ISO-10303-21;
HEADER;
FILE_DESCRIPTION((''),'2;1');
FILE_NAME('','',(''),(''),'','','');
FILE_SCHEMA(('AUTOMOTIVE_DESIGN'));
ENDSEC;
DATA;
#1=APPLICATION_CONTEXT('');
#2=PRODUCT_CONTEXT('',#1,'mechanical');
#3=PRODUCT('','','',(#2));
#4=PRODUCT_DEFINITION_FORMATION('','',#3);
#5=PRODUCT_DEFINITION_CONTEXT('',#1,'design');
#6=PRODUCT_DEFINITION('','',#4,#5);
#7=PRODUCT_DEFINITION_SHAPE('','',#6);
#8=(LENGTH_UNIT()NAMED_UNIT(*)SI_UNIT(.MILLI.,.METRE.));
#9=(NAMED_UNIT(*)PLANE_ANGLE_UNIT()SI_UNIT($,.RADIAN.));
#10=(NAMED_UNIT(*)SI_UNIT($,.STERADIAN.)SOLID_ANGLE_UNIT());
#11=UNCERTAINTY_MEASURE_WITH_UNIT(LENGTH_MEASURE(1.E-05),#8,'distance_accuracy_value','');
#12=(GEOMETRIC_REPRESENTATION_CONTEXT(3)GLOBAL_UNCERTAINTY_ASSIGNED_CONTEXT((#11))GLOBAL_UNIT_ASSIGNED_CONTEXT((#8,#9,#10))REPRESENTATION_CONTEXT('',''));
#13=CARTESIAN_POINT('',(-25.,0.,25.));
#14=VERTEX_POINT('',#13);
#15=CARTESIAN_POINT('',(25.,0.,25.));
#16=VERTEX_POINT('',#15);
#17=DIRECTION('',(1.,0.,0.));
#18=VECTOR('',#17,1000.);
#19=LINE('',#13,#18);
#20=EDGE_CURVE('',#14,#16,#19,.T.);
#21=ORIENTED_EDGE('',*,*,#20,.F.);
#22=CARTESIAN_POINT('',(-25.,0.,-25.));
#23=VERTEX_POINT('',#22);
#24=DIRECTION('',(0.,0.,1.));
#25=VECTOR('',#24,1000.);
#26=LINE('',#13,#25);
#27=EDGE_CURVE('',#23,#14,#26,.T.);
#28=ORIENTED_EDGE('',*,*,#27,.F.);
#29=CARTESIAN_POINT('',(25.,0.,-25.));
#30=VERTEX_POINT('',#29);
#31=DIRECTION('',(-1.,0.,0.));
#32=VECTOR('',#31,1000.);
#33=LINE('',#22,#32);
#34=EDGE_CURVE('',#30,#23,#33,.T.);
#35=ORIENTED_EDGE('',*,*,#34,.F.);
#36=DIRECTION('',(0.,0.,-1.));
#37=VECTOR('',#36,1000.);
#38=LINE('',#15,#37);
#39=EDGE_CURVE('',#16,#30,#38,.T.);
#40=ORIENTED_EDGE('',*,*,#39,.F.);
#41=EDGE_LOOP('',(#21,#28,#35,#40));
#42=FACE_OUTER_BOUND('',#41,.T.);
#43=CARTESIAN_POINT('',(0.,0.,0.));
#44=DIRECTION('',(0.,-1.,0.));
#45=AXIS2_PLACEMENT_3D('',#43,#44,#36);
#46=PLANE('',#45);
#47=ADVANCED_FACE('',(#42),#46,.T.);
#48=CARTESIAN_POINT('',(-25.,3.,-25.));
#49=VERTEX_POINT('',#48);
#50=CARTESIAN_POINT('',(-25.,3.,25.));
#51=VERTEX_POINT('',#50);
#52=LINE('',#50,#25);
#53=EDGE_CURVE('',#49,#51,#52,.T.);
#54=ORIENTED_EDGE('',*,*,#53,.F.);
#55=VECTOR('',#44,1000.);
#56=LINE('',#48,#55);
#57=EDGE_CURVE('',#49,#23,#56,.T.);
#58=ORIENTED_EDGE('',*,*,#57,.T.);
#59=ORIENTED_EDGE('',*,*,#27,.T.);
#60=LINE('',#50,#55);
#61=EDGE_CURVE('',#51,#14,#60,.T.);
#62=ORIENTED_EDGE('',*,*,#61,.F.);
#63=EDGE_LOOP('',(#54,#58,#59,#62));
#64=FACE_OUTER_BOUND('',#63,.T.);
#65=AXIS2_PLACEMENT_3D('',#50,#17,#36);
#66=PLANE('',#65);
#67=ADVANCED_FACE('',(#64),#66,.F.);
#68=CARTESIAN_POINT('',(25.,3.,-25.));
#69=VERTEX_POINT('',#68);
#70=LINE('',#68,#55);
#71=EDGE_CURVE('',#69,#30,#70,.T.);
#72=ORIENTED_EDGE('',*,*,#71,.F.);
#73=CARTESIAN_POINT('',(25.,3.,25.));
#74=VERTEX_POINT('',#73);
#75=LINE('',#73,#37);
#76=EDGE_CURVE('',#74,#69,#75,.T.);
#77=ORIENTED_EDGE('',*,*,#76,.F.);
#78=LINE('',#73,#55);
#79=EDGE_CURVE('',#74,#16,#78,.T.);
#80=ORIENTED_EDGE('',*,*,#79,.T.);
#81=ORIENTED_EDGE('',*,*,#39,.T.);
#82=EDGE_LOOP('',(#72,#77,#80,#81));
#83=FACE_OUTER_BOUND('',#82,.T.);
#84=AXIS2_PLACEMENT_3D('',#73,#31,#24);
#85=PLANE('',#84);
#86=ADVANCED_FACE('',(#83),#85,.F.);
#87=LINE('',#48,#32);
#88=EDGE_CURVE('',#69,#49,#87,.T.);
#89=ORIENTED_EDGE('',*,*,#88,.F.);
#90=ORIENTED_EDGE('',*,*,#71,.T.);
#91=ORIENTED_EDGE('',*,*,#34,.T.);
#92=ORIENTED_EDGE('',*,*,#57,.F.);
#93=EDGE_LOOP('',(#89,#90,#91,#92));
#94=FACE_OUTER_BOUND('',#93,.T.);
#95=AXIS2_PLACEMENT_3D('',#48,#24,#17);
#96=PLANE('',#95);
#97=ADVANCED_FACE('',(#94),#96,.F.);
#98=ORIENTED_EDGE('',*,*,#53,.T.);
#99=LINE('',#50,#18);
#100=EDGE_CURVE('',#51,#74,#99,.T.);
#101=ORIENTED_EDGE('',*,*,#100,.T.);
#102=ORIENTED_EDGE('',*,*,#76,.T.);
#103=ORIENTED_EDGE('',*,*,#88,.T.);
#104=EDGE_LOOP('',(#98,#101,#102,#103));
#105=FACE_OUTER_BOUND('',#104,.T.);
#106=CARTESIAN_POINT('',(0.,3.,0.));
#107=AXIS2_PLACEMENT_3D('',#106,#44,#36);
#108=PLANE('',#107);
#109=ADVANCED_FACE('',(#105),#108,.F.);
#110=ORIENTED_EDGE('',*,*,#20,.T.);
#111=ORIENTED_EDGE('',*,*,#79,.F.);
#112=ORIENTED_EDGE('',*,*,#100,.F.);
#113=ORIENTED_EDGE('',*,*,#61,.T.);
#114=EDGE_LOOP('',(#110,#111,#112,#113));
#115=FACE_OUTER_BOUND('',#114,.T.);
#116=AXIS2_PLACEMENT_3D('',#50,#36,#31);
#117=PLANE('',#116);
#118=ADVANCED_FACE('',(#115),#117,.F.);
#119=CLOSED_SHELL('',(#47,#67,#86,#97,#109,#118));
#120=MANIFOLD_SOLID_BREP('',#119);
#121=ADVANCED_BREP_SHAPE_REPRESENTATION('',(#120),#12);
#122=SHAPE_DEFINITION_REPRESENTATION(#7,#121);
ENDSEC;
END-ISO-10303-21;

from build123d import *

# Parameters (mm, degrees)
SKETCH1_W           = 50
SKETCH1_H           = 50
BOSS_EXTRUDE1_DEPTH = 3


with BuildPart() as part:
    # Sketch1 → Boss-Extrude1 (new body)
    with BuildSketch(Plane(origin=(0, 0, 0), x_dir=(1, 0, 0), z_dir=(0, 1, 0))):
        Rectangle(SKETCH1_W, SKETCH1_H)
    extrude(amount=BOSS_EXTRUDE1_DEPTH)


solid = part.part
